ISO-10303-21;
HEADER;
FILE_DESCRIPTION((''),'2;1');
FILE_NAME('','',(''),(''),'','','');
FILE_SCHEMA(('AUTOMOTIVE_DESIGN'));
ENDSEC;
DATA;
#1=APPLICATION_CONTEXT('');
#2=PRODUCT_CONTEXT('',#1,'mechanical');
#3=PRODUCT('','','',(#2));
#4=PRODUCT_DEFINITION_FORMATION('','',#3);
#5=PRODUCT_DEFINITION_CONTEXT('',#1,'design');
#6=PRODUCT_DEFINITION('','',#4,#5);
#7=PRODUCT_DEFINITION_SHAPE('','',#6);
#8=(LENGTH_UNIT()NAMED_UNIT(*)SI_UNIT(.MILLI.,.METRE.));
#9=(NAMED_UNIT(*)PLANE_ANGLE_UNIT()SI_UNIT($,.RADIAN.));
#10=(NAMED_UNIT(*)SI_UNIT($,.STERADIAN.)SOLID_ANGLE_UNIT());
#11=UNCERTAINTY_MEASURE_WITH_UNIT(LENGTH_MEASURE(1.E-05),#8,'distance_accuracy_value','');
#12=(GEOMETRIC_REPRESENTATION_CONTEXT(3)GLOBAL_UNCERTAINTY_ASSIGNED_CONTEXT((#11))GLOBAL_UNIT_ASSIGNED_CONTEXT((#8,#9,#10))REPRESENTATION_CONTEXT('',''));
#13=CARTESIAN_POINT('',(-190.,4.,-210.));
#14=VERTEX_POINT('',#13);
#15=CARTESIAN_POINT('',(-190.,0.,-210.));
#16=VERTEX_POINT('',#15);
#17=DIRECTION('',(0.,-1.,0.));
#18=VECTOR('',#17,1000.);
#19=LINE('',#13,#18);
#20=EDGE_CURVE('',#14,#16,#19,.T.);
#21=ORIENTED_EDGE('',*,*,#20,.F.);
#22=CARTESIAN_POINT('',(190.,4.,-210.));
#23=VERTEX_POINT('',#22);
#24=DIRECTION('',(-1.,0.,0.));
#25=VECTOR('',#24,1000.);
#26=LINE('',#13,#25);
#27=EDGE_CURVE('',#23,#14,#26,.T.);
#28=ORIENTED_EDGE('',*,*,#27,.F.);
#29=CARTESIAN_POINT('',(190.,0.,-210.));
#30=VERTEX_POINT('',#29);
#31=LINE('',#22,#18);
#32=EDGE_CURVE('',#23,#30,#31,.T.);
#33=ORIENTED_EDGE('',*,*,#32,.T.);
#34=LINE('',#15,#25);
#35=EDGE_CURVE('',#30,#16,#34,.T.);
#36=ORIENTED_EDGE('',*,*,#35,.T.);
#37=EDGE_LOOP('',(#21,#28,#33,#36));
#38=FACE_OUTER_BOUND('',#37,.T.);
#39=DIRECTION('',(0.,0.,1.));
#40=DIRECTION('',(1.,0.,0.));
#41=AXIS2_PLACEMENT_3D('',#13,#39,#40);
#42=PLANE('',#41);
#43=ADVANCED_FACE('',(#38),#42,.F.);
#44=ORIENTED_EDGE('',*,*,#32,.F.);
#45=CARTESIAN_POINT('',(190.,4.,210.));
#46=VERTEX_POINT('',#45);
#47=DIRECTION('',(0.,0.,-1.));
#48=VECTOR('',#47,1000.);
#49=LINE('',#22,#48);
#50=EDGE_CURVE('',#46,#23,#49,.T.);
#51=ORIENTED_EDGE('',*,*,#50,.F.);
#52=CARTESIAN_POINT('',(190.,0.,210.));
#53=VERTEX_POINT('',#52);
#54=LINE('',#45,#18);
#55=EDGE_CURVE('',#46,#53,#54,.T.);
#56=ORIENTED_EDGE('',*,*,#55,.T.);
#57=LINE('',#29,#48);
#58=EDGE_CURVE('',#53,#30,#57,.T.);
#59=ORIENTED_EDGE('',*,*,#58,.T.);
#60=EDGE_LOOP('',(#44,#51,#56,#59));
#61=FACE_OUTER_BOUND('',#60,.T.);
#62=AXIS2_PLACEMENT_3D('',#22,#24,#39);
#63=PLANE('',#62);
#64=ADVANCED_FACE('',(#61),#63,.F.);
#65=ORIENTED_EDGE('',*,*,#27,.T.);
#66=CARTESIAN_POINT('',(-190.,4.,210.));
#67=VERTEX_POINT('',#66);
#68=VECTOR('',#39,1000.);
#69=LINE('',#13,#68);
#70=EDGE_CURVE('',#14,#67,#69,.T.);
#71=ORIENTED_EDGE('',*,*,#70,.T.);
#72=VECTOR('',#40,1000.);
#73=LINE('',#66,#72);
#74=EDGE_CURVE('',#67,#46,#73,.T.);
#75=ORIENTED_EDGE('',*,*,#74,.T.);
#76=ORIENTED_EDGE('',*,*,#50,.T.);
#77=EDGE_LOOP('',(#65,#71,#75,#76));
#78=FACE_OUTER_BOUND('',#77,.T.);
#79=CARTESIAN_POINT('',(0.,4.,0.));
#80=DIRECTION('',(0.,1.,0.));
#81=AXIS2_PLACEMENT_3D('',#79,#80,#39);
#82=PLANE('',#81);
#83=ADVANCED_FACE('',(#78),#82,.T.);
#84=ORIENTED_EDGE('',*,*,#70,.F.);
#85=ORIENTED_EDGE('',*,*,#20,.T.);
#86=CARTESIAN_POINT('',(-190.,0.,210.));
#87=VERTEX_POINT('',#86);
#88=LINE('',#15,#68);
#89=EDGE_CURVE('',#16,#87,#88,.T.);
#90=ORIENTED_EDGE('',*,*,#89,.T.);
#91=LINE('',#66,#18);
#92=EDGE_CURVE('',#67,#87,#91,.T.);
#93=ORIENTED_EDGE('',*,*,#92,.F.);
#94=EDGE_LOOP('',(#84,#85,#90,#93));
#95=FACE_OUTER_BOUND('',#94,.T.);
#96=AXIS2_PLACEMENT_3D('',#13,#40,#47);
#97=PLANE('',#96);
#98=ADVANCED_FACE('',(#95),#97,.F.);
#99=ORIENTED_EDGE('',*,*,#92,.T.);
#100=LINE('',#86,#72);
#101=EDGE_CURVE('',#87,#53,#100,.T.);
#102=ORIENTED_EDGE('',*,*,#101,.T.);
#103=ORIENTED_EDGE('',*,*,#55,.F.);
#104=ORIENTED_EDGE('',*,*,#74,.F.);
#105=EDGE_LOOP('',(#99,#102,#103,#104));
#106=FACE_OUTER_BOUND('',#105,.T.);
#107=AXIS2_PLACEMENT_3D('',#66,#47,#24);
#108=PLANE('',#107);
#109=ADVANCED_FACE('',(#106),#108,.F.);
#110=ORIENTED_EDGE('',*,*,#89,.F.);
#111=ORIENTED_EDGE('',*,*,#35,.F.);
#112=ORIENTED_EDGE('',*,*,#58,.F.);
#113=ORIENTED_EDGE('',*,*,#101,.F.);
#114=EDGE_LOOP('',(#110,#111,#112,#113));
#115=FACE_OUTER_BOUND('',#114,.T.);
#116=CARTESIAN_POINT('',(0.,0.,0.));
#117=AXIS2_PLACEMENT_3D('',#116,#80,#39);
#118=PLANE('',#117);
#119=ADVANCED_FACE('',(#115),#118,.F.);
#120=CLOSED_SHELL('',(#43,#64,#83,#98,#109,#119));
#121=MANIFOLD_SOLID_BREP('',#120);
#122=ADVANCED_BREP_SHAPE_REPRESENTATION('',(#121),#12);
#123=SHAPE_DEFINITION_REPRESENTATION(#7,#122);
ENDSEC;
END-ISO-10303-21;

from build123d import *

# Parameters (mm, degrees)
SKETCH1_W           = 380
SKETCH1_H           = 420
BOSS_EXTRUDE1_DEPTH = 4


with BuildPart() as part:
    # Sketch1 → Boss-Extrude1 (new body)
    with BuildSketch(Plane(origin=(0, 0, 0), x_dir=(1, 0, 0), z_dir=(0, 1, 0))):
        Rectangle(SKETCH1_W, SKETCH1_H)
    extrude(amount=BOSS_EXTRUDE1_DEPTH)


solid = part.part
